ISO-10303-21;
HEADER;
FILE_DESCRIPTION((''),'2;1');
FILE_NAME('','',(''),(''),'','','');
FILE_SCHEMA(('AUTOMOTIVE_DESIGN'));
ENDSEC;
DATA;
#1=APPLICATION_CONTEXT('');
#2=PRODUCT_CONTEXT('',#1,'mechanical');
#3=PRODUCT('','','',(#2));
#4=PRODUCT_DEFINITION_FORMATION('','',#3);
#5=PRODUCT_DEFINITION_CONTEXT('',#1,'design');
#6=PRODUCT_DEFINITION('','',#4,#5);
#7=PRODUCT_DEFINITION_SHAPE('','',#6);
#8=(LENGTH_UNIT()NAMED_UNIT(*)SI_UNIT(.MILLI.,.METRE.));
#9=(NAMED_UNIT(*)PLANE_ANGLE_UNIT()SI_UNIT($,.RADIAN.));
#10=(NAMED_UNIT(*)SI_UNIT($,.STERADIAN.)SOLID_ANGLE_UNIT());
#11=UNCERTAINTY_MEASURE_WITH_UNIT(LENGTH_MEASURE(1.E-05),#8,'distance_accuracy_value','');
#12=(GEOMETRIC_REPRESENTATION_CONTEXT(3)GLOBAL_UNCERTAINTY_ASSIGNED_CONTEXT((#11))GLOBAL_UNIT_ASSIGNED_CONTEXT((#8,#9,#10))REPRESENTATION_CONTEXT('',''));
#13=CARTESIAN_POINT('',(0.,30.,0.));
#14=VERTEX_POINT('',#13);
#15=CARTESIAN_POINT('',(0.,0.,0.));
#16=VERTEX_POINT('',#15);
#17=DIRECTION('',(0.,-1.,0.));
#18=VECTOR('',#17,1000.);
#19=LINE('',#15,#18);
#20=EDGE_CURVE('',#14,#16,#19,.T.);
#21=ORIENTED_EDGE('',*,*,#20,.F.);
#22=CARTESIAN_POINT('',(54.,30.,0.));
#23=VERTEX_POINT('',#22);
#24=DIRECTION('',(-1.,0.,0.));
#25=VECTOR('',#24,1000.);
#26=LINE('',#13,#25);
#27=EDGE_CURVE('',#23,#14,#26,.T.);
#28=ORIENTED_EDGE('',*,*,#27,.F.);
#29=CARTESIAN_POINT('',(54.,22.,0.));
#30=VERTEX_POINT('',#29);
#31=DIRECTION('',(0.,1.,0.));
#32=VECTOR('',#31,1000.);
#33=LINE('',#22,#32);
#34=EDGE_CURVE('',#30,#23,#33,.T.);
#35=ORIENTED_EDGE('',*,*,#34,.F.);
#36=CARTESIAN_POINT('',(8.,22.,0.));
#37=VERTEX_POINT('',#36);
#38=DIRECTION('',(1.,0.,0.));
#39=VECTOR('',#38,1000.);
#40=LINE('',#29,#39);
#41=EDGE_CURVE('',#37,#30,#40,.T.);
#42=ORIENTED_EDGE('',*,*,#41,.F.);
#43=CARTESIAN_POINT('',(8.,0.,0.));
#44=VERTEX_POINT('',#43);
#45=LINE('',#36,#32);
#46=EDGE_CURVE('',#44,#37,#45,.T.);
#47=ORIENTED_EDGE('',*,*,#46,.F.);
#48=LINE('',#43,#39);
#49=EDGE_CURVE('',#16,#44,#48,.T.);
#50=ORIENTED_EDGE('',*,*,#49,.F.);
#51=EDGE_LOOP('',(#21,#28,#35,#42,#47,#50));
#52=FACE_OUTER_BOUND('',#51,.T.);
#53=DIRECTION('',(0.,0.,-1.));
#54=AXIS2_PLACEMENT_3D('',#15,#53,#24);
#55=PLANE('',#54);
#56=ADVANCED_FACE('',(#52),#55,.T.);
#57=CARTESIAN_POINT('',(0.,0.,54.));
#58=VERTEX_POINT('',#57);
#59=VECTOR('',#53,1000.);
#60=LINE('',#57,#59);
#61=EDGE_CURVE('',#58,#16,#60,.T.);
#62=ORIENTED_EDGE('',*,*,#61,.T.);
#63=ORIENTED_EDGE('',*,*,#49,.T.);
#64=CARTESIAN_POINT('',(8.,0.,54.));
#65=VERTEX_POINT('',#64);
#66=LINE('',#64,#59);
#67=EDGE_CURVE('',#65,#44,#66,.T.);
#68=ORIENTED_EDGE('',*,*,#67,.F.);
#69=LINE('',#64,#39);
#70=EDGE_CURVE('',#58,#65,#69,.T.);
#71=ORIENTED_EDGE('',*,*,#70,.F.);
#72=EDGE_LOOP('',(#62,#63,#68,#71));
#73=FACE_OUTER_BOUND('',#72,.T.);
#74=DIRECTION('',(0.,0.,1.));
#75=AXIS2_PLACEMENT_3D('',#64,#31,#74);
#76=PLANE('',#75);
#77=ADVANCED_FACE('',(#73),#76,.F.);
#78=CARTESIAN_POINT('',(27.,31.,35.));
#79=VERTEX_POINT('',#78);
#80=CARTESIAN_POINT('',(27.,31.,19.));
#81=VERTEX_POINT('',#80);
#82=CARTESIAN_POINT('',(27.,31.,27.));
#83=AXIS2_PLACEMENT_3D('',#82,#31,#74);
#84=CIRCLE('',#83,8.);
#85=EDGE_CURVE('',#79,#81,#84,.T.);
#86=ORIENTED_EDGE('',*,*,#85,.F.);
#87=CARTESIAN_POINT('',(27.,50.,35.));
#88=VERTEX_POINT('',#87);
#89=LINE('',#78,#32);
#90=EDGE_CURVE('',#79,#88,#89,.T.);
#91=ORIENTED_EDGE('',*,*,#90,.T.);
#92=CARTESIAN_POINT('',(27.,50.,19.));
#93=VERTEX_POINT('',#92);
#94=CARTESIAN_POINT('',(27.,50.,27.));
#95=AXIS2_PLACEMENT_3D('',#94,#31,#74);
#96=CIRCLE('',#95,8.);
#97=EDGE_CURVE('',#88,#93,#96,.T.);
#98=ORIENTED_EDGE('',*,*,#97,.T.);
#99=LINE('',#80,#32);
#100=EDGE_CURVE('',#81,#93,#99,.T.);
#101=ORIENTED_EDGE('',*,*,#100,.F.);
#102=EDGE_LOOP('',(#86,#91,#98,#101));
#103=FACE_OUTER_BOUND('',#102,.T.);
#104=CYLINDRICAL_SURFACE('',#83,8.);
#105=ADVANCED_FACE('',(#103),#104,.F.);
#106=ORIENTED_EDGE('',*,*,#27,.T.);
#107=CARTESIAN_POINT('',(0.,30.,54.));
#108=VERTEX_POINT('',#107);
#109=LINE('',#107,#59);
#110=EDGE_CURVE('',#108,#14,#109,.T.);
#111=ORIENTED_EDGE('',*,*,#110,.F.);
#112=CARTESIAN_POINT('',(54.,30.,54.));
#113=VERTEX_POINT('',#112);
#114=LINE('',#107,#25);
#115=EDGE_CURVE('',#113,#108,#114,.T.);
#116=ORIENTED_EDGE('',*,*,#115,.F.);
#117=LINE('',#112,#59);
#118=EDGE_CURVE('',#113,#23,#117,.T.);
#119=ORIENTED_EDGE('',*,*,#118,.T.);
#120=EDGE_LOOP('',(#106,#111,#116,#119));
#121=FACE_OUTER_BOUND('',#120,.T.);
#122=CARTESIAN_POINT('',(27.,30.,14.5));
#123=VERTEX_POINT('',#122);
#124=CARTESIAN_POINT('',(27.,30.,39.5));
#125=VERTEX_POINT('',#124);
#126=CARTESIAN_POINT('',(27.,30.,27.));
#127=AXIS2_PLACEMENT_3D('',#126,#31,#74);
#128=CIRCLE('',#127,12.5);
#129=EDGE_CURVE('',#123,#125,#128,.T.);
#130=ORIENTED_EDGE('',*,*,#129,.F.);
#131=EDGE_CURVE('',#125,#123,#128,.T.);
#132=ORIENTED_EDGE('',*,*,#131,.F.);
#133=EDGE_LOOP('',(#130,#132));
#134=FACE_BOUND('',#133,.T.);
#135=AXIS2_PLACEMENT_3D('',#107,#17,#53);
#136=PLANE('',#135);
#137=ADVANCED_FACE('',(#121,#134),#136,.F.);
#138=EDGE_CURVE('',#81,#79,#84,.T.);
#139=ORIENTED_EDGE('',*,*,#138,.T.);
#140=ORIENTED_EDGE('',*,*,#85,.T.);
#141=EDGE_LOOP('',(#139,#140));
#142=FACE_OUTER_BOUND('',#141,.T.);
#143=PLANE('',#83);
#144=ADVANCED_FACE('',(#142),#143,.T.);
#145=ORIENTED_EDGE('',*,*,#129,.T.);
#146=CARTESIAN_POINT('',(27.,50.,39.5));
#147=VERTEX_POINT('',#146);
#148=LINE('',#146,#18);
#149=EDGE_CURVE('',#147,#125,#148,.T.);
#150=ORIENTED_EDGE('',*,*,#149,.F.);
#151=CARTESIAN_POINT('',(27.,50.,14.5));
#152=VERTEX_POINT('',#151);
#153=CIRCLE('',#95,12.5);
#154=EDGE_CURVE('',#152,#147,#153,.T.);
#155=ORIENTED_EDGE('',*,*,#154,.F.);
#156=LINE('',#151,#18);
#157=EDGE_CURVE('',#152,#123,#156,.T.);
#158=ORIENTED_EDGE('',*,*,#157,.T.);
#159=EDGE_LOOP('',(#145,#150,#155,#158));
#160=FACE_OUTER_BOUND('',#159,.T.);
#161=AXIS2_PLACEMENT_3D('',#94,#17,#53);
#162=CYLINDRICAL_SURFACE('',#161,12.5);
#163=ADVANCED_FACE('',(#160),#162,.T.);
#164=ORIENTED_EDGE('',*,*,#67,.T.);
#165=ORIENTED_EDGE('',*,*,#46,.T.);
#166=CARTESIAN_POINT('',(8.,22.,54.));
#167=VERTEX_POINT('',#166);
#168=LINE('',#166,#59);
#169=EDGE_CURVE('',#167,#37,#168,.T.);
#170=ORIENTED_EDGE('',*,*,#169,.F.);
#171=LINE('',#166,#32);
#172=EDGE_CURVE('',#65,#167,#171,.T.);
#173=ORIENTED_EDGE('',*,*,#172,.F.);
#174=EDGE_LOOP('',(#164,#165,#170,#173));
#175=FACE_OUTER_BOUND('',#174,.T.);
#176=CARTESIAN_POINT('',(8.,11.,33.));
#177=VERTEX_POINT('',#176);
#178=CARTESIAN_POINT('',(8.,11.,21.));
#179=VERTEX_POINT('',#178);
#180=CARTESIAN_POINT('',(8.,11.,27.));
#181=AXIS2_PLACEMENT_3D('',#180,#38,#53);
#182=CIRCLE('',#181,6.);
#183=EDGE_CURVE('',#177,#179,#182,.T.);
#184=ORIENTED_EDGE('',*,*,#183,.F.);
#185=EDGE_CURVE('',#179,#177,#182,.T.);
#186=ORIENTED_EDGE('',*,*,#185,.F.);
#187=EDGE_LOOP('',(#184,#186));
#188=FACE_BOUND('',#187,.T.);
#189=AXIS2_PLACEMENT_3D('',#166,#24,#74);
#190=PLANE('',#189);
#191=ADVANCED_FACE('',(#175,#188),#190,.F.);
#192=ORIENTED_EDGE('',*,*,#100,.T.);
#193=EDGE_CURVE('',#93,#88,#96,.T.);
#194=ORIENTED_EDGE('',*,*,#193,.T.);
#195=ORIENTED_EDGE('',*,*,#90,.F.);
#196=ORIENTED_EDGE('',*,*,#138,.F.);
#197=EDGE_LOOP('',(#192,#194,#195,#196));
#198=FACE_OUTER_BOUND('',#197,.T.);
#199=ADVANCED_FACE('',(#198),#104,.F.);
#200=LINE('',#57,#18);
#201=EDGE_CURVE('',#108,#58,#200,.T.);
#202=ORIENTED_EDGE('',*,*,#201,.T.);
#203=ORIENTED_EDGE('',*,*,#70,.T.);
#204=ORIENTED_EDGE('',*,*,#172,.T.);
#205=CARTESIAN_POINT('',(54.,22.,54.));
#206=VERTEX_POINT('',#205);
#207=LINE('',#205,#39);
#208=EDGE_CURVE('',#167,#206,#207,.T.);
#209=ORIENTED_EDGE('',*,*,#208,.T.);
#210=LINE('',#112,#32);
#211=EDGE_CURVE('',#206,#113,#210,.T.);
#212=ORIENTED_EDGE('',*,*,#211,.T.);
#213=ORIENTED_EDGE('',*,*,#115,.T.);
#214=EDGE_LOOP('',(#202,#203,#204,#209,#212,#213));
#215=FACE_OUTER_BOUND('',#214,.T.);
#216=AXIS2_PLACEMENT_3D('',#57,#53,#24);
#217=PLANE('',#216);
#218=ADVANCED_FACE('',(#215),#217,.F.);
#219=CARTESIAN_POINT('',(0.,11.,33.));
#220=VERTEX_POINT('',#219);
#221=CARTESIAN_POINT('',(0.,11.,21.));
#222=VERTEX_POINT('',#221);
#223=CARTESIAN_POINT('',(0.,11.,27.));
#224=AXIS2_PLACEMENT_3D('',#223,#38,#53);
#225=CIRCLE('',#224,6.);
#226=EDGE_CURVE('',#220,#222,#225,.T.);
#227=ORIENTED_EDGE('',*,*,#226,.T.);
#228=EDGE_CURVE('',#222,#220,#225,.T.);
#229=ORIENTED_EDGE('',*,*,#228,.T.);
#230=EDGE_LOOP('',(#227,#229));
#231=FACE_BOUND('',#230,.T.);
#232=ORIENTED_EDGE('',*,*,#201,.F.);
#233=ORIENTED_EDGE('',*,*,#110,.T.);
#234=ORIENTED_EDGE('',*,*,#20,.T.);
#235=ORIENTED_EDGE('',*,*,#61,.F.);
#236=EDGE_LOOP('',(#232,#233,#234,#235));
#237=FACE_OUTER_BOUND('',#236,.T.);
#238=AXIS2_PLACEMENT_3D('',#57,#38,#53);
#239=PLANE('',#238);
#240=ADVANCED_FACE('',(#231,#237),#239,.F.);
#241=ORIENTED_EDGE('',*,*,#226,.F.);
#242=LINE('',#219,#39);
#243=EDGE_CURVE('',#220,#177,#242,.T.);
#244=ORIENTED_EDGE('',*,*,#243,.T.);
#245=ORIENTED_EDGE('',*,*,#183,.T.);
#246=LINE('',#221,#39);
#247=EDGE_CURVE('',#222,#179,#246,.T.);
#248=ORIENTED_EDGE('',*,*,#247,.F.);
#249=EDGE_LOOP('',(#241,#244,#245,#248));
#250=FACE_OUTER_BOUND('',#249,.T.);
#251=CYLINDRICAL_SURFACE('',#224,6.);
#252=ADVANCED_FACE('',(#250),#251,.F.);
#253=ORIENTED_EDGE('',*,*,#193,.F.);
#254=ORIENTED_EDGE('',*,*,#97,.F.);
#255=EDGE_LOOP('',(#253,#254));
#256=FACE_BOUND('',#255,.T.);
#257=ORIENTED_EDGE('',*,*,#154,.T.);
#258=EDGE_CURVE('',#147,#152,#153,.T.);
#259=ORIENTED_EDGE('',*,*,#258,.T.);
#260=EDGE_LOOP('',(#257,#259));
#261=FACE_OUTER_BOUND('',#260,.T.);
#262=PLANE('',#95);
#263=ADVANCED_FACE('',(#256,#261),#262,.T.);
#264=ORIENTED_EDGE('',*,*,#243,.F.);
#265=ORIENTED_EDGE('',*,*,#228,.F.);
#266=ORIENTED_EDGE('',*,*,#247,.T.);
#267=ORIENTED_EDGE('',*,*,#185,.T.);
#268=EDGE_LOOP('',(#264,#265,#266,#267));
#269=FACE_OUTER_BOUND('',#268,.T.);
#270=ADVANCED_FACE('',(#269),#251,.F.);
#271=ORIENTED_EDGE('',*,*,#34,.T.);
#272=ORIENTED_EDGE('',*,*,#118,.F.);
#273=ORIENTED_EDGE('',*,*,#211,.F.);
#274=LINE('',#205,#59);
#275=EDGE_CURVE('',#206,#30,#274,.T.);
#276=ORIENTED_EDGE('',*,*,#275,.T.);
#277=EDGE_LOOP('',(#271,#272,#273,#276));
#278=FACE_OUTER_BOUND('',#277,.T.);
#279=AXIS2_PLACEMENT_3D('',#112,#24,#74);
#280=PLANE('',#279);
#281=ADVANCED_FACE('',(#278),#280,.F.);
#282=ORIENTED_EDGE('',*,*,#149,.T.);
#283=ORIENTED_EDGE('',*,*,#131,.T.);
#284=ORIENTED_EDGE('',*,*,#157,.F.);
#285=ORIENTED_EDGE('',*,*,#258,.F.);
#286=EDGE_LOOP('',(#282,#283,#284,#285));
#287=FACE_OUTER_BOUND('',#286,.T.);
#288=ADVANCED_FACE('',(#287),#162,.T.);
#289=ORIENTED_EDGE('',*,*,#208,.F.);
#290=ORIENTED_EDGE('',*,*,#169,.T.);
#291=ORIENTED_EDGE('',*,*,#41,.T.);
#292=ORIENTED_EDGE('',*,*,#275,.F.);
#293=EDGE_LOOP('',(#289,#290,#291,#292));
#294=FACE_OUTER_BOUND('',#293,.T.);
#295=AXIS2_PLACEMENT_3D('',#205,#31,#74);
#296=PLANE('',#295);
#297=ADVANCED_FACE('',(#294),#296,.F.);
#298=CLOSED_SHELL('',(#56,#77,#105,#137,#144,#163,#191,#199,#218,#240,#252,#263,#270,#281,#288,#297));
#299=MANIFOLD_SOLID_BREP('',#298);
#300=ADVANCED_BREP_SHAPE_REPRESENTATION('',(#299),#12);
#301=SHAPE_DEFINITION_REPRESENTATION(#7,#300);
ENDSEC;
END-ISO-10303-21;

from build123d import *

# Parameters (mm, degrees)
BRACKET_BODY_DEPTH = 54
BOSS_SKETCH_R      = 12.5
BOSS_25_DEPTH      = 20
BORE_SKETCH_R      = 8
BORE_16_DEPTH      = 19
HOLE_SKETCH_R      = 6
HOLE_12_DEPTH      = 8


with BuildPart() as part:
    # Bracket Profile Sketch → Bracket Body (new body)
    with BuildSketch(Plane.XY):
        Polygon((0, 0), (0, 30), (54, 30), (54, 22), (8, 22), (8, 0), align=None)
    extrude(amount=BRACKET_BODY_DEPTH)

    # Boss Sketch → Boss Ø25 (add)
    with BuildSketch(Plane(origin=(0, 30, 0), x_dir=(1, 0, 0), z_dir=(0, 1, 0))):
        with Locations(Location((27, -27, 0), (0, 0, 270))):
            Circle(BOSS_SKETCH_R)
    extrude(amount=BOSS_25_DEPTH)

    # Bore Sketch → Bore Ø16 (cut)
    with BuildSketch(Plane(origin=(0, 50, 0), x_dir=(1, 0, 0), z_dir=(0, 1, 0))):
        with Locations(Location((27, -27, 0), (0, 0, 270))):
            Circle(BORE_SKETCH_R)
    extrude(amount=-BORE_16_DEPTH, mode=Mode.SUBTRACT)

    # Hole Sketch → Hole Ø12 (cut)
    with BuildSketch(Plane(origin=(8, 0, 0), x_dir=(0, 0, -1), z_dir=(1, 0, 0))):
        with Locations((-27, 11)):
            Circle(HOLE_SKETCH_R)
    extrude(amount=-HOLE_12_DEPTH, mode=Mode.SUBTRACT)


solid = part.part
